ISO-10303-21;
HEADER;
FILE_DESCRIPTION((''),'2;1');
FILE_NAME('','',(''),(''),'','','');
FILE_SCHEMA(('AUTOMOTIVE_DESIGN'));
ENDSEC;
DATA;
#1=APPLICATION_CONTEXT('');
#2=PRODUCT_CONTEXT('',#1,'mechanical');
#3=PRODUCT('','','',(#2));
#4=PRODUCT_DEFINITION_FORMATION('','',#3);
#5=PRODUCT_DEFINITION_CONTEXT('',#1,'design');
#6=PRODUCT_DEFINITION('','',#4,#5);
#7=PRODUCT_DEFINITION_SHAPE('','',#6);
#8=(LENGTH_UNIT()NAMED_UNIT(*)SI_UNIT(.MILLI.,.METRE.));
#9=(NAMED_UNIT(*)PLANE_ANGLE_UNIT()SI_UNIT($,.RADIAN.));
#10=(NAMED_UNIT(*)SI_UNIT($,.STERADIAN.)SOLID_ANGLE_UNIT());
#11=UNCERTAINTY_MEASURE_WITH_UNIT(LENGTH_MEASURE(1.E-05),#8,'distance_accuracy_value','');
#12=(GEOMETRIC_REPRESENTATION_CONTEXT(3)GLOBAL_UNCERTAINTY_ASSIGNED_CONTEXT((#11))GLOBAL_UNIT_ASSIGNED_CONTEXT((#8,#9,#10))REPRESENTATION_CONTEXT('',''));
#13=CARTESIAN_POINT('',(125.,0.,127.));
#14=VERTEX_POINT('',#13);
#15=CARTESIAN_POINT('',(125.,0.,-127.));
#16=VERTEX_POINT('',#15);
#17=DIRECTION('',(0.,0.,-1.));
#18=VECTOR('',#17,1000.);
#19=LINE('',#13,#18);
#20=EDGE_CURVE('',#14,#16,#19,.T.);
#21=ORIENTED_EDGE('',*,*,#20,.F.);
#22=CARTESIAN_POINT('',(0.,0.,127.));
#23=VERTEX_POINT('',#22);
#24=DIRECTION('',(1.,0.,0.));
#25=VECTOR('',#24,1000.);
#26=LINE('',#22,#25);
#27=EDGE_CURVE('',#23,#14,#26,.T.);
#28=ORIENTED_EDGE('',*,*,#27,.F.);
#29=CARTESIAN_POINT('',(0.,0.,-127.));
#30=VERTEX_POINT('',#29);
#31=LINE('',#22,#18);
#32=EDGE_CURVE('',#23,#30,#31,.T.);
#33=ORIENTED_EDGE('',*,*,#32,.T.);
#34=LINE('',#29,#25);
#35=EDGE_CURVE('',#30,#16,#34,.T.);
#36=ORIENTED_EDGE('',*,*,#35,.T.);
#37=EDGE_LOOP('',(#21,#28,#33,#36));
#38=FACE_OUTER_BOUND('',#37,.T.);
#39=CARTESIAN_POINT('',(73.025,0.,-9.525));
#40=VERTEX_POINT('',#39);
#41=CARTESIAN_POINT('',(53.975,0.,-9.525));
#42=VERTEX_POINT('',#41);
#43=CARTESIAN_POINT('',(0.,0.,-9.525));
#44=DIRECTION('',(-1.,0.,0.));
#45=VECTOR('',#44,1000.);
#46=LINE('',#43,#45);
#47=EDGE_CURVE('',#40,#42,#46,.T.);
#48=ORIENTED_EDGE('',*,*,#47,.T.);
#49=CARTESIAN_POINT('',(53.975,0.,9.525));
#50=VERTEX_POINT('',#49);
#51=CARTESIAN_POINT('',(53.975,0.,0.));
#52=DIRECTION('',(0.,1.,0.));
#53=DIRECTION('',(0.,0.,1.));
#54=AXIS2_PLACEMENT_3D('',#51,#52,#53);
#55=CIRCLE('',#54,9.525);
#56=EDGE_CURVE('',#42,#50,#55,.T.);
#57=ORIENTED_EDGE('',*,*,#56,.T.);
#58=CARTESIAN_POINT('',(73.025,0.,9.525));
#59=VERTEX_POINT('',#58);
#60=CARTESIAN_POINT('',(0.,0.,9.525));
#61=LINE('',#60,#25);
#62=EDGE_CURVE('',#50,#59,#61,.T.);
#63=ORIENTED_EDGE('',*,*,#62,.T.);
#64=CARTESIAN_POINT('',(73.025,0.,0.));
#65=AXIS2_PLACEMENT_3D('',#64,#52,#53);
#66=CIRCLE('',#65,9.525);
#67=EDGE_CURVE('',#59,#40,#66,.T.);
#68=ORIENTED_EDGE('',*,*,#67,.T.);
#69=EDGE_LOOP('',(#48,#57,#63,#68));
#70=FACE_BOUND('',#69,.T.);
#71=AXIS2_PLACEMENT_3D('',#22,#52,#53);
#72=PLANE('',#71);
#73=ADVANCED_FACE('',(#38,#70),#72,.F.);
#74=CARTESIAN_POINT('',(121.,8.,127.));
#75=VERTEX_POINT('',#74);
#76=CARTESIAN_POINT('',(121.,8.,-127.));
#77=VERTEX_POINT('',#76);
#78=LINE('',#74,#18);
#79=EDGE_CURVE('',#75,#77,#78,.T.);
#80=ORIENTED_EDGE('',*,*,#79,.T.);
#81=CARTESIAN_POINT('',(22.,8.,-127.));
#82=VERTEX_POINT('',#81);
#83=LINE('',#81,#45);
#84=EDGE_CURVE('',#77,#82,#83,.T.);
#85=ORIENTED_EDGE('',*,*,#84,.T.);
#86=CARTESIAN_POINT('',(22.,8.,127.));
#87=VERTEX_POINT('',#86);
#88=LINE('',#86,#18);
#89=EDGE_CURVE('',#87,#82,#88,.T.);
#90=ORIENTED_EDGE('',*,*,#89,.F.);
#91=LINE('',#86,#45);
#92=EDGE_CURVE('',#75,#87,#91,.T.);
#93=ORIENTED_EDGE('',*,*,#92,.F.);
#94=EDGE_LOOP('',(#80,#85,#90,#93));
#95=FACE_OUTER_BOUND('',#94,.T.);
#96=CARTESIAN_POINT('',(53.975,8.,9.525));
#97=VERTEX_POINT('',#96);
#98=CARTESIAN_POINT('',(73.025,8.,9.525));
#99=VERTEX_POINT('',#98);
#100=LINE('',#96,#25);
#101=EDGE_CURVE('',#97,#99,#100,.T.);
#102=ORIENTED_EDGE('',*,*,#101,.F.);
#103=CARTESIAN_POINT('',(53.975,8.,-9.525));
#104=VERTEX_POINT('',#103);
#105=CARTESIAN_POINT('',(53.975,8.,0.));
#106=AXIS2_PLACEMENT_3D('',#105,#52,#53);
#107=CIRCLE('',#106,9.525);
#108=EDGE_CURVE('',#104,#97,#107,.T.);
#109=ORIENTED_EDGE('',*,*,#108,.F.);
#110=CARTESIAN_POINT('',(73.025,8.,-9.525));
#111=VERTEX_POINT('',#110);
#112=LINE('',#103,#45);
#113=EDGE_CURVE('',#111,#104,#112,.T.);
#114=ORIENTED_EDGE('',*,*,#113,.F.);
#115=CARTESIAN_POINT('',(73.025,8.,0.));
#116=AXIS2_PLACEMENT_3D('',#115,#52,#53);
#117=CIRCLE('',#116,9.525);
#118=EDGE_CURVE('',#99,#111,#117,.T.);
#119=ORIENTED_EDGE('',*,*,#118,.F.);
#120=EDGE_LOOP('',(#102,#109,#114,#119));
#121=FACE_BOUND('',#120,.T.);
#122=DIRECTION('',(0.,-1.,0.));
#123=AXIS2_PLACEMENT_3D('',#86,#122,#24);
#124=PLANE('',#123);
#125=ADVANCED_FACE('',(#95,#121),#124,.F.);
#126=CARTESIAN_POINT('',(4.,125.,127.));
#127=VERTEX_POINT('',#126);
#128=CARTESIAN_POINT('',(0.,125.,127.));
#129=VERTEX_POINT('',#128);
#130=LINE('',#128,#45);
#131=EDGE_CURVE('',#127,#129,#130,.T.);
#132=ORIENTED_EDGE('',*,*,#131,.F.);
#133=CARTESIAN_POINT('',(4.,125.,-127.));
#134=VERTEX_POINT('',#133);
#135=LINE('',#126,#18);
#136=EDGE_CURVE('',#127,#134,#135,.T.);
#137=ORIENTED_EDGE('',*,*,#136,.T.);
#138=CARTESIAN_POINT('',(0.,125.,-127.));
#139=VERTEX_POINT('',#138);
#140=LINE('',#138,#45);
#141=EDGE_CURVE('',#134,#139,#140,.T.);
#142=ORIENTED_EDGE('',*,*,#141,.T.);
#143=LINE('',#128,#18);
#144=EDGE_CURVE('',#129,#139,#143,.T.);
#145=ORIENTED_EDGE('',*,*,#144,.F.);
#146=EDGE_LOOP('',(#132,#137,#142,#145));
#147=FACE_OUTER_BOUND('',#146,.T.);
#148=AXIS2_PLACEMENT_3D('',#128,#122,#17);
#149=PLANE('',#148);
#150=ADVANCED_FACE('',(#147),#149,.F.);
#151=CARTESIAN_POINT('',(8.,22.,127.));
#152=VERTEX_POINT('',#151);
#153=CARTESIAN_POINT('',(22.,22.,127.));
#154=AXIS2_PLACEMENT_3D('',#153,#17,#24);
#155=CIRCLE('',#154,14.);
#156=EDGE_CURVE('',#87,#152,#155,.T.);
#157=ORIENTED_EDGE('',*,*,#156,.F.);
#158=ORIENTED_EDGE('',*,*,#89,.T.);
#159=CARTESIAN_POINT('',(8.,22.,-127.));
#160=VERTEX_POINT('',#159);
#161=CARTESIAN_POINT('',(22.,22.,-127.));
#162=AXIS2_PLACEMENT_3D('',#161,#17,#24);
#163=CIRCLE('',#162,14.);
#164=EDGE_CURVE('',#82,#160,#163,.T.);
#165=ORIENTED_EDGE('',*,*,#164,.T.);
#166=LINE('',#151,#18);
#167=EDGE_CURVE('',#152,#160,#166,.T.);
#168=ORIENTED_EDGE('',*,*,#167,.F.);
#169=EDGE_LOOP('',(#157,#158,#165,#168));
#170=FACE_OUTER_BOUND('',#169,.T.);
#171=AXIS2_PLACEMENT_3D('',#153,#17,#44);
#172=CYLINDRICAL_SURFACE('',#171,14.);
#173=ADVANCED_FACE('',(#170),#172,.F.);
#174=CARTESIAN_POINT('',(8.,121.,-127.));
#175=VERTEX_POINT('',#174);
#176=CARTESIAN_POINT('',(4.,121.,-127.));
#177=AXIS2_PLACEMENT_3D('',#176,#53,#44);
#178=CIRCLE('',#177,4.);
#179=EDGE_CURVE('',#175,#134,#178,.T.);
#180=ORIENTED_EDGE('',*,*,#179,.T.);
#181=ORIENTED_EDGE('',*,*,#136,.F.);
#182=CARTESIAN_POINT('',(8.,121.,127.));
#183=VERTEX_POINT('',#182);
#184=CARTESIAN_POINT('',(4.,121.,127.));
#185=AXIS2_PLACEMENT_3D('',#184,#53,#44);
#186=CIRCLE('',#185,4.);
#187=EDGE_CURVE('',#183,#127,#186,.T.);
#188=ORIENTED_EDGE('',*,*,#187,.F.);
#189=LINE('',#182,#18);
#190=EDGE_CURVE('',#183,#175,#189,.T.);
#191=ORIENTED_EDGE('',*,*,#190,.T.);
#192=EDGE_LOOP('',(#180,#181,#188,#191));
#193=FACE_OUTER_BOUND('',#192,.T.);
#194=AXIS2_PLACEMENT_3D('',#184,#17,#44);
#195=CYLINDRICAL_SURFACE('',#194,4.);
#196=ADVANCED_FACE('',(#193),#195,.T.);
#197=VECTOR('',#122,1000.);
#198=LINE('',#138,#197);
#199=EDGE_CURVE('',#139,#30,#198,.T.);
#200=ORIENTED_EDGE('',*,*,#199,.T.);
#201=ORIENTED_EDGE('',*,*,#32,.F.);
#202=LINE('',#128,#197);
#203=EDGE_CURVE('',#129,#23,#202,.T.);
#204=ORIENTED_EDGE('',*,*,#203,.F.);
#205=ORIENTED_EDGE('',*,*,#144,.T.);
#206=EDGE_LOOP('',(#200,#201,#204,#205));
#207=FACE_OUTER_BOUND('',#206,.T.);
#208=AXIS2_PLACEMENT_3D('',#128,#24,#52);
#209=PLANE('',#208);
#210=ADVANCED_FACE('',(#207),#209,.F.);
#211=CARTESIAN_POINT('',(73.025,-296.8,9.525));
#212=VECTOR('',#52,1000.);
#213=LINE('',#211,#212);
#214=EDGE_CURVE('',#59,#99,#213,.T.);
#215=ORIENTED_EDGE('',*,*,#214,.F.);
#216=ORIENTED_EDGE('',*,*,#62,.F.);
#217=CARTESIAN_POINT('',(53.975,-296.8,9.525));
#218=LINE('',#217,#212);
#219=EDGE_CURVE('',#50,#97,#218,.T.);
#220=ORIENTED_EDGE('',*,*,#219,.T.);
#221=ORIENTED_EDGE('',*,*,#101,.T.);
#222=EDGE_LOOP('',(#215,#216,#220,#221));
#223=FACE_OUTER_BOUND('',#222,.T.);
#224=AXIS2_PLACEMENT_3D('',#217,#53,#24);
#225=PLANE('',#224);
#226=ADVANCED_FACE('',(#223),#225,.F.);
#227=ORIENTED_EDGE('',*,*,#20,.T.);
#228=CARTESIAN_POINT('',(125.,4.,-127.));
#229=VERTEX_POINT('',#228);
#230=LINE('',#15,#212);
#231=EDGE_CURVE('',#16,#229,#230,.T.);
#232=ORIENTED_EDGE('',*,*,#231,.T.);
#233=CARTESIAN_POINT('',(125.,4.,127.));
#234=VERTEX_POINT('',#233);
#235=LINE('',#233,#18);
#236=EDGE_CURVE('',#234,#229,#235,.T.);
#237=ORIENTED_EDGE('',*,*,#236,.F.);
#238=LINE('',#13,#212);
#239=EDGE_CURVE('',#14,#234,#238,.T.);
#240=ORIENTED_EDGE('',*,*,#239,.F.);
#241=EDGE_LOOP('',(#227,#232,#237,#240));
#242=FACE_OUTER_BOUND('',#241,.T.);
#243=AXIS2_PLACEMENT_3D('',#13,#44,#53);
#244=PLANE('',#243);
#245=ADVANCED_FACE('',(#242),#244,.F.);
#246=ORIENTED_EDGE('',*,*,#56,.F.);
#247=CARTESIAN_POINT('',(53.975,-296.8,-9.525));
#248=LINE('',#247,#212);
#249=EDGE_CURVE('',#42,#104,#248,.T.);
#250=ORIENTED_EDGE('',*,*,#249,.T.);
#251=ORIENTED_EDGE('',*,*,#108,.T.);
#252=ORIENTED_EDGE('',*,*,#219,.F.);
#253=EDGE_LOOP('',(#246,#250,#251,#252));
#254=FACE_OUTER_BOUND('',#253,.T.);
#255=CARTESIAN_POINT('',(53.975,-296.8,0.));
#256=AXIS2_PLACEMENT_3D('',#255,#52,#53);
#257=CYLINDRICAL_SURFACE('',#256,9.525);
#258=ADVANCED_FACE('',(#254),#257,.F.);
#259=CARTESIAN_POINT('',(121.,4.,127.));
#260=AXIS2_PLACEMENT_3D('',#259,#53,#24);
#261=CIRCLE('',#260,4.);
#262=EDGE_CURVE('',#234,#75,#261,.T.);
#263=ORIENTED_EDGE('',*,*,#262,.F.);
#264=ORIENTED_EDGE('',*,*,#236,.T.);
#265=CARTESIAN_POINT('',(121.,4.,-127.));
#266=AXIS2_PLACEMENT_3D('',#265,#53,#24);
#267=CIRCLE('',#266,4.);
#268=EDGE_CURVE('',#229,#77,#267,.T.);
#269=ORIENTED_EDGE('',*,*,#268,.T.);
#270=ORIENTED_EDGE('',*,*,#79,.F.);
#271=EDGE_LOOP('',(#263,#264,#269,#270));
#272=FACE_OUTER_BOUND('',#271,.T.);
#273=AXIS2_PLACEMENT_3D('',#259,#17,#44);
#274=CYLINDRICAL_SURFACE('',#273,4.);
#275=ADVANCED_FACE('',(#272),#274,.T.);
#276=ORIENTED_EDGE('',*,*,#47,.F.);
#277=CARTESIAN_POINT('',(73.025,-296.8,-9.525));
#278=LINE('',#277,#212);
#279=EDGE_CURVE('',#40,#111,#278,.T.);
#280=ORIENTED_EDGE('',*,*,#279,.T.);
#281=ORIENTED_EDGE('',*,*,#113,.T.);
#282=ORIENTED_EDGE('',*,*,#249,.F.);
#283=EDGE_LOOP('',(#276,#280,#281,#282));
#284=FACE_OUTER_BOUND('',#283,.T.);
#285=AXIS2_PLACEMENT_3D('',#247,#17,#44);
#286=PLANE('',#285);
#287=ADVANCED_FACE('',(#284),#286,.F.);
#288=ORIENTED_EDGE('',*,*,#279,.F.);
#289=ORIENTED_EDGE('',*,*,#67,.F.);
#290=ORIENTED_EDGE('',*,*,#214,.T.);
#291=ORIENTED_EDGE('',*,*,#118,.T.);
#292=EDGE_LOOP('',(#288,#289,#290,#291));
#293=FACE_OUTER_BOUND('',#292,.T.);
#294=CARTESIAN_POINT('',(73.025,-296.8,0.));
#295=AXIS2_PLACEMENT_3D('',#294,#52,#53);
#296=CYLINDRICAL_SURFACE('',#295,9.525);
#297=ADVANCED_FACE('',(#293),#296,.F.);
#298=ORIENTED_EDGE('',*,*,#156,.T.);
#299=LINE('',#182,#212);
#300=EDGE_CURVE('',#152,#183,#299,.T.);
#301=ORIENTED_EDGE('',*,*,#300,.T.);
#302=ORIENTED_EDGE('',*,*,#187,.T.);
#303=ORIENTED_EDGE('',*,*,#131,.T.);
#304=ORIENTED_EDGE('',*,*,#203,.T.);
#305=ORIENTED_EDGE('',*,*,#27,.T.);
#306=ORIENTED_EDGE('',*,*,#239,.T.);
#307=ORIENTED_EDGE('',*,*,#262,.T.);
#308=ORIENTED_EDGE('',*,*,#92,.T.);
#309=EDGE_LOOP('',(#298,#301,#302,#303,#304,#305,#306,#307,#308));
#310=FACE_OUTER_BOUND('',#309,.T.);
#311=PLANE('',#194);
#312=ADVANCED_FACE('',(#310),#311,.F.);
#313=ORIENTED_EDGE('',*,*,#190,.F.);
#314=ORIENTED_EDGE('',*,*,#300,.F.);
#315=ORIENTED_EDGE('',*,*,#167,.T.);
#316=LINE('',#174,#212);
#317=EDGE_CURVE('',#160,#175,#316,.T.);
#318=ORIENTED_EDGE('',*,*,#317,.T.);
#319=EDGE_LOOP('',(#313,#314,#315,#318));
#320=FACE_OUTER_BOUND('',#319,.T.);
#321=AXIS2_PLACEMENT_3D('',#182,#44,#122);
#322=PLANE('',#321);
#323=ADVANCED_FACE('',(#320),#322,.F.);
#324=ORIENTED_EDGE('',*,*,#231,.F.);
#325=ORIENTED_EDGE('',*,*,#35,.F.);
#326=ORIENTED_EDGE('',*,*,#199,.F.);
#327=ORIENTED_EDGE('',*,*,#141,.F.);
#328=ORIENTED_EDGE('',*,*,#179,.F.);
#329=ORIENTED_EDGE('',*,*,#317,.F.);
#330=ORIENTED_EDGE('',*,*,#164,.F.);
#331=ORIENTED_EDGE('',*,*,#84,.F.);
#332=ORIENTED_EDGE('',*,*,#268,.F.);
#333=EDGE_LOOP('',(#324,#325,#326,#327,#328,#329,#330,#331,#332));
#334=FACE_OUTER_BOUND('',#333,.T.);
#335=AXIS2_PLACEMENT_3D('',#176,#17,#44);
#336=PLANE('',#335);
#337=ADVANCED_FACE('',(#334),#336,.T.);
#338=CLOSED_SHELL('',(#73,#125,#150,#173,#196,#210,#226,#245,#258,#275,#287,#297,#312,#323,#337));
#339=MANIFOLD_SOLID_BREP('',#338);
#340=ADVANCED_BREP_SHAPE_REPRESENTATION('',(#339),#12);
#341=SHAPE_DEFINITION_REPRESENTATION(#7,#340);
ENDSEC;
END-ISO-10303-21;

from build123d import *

# Parameters (mm, degrees)
BOSS_EXTRUDE1_DEPTH = 127
CUT_EXTRUDE1_DEPTH  = 304.8


with BuildPart() as part:
    # Sketch1 → Boss-Extrude1 (new, symmetric)
    with BuildSketch(Plane.XY):
        with BuildLine():
            Line((0, 125), (0, 0))
            Line((0, 0), (125, 0))
            Line((125, 0), (125, 4))
            ThreePointArc((125, 4), (123.828427125, 6.828427125), (121, 8))
            Line((121, 8), (22, 8))
            ThreePointArc((22, 8), (12.100505063, 12.100505063), (8, 22))
            Line((8, 22), (8, 121))
            ThreePointArc((8, 121), (6.828427125, 123.828427125), (4, 125))
            Line((4, 125), (0, 125))
        make_face()
    extrude(amount=BOSS_EXTRUDE1_DEPTH, both=True)

    # Sketch2 → Cut-Extrude1 (cut)
    with BuildSketch(Plane(origin=(0, 8, 0), x_dir=(1, 0, 0), z_dir=(0, 1, 0))):
        with BuildLine():
            Line((53.975, 9.525), (73.025, 9.525))
            ThreePointArc((73.025, 9.525), (82.55, 0), (73.025, -9.525))
            Line((73.025, -9.525), (53.975, -9.525))
            ThreePointArc((53.975, -9.525), (44.45, 0), (53.975, 9.525))
        make_face()
    extrude(amount=-CUT_EXTRUDE1_DEPTH, mode=Mode.SUBTRACT)


solid = part.part
